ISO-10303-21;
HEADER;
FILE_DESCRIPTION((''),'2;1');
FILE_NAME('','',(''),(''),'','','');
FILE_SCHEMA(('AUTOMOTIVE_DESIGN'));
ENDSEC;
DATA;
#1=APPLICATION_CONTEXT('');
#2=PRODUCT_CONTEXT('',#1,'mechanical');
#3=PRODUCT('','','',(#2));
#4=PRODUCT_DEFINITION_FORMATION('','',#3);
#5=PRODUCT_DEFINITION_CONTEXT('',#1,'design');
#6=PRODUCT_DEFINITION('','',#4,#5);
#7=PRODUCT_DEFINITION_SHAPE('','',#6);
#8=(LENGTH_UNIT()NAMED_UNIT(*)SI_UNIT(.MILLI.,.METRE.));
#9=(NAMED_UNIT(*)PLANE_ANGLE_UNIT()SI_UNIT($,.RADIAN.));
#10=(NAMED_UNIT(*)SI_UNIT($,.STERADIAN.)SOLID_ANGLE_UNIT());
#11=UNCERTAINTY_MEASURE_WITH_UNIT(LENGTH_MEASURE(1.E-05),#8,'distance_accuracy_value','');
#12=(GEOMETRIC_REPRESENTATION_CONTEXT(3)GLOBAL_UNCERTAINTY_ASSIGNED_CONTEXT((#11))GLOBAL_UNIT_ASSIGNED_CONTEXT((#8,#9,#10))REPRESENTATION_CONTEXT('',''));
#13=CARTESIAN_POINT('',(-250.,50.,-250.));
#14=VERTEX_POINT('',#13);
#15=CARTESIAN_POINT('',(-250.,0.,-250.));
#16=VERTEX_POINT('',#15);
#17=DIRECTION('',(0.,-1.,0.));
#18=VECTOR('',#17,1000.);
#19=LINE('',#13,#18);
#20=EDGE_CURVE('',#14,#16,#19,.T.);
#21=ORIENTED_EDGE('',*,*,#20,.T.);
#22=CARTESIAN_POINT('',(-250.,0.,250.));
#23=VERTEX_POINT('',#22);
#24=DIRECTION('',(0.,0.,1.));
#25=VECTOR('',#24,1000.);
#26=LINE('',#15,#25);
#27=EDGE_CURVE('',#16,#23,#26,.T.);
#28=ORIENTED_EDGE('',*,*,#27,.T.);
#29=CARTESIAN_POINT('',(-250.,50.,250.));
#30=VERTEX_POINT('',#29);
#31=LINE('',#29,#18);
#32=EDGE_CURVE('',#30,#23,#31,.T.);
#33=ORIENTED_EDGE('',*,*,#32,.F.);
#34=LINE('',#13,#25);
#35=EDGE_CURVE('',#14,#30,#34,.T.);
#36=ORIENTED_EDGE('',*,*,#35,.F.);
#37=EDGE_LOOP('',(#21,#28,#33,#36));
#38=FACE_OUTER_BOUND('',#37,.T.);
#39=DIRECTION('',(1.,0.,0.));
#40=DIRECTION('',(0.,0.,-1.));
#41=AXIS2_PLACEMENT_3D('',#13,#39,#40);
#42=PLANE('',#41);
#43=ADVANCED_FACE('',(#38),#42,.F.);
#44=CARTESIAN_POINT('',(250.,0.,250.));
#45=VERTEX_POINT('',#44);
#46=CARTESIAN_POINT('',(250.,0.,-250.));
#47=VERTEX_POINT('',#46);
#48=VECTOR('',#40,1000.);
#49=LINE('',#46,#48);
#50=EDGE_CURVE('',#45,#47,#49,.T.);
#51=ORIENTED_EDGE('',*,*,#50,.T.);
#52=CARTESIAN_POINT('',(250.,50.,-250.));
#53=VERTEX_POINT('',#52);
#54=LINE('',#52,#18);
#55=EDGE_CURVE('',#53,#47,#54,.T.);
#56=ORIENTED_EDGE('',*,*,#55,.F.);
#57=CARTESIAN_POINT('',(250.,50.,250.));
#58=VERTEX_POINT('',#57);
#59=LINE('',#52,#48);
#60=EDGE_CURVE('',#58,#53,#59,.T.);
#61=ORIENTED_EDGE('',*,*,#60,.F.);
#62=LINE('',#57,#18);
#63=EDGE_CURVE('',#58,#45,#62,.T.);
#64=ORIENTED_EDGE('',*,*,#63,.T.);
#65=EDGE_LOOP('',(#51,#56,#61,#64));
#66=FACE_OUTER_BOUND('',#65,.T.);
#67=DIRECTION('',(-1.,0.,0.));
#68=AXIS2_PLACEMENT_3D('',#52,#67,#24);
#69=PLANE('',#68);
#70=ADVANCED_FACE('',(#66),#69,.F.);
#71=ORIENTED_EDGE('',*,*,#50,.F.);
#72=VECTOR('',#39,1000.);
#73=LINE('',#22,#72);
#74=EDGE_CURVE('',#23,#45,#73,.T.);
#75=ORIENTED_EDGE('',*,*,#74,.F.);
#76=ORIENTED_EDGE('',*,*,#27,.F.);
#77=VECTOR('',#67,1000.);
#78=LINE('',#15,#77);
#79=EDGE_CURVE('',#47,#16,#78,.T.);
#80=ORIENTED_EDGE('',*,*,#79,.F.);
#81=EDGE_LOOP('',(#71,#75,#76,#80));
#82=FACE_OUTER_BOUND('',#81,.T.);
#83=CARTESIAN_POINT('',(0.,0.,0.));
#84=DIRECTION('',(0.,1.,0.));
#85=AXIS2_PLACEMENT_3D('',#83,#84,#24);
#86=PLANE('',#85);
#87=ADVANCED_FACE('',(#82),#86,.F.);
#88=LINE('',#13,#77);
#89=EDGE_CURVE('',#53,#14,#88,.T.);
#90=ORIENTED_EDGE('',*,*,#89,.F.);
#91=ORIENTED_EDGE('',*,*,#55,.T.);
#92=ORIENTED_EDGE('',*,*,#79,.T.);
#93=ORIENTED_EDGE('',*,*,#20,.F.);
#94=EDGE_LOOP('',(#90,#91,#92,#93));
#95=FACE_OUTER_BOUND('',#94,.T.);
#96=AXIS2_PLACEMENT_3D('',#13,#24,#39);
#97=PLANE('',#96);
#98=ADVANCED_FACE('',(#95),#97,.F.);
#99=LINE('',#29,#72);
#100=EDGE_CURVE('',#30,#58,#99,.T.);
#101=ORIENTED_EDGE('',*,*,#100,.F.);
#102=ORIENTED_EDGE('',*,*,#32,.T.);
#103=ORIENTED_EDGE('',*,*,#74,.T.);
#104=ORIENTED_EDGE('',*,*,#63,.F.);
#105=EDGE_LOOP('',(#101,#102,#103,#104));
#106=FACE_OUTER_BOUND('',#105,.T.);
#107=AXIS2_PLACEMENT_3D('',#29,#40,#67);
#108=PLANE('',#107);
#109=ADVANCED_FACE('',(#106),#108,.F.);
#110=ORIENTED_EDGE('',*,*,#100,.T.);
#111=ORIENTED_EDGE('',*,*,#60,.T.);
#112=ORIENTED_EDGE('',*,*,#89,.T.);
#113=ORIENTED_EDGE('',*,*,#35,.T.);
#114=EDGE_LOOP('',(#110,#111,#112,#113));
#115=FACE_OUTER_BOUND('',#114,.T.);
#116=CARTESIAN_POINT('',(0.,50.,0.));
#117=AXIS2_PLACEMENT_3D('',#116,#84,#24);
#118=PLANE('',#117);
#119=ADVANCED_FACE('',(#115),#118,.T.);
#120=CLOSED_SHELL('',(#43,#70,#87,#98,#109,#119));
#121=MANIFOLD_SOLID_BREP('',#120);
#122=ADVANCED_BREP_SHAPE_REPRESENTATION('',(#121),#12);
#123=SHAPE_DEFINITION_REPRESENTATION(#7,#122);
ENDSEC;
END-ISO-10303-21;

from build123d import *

# Parameters (mm, degrees)
SKETCH_1_W      = 500
SKETCH_1_H      = 500
EXTRUDE_1_DEPTH = 50


with BuildPart() as part:
    # 草图1 → 凸台-拉伸1 (new body)
    with BuildSketch(Plane(origin=(0, 0, 0), x_dir=(1, 0, 0), z_dir=(0, 1, 0))):
        Rectangle(SKETCH_1_W, SKETCH_1_H)
    extrude(amount=EXTRUDE_1_DEPTH)


solid = part.part
